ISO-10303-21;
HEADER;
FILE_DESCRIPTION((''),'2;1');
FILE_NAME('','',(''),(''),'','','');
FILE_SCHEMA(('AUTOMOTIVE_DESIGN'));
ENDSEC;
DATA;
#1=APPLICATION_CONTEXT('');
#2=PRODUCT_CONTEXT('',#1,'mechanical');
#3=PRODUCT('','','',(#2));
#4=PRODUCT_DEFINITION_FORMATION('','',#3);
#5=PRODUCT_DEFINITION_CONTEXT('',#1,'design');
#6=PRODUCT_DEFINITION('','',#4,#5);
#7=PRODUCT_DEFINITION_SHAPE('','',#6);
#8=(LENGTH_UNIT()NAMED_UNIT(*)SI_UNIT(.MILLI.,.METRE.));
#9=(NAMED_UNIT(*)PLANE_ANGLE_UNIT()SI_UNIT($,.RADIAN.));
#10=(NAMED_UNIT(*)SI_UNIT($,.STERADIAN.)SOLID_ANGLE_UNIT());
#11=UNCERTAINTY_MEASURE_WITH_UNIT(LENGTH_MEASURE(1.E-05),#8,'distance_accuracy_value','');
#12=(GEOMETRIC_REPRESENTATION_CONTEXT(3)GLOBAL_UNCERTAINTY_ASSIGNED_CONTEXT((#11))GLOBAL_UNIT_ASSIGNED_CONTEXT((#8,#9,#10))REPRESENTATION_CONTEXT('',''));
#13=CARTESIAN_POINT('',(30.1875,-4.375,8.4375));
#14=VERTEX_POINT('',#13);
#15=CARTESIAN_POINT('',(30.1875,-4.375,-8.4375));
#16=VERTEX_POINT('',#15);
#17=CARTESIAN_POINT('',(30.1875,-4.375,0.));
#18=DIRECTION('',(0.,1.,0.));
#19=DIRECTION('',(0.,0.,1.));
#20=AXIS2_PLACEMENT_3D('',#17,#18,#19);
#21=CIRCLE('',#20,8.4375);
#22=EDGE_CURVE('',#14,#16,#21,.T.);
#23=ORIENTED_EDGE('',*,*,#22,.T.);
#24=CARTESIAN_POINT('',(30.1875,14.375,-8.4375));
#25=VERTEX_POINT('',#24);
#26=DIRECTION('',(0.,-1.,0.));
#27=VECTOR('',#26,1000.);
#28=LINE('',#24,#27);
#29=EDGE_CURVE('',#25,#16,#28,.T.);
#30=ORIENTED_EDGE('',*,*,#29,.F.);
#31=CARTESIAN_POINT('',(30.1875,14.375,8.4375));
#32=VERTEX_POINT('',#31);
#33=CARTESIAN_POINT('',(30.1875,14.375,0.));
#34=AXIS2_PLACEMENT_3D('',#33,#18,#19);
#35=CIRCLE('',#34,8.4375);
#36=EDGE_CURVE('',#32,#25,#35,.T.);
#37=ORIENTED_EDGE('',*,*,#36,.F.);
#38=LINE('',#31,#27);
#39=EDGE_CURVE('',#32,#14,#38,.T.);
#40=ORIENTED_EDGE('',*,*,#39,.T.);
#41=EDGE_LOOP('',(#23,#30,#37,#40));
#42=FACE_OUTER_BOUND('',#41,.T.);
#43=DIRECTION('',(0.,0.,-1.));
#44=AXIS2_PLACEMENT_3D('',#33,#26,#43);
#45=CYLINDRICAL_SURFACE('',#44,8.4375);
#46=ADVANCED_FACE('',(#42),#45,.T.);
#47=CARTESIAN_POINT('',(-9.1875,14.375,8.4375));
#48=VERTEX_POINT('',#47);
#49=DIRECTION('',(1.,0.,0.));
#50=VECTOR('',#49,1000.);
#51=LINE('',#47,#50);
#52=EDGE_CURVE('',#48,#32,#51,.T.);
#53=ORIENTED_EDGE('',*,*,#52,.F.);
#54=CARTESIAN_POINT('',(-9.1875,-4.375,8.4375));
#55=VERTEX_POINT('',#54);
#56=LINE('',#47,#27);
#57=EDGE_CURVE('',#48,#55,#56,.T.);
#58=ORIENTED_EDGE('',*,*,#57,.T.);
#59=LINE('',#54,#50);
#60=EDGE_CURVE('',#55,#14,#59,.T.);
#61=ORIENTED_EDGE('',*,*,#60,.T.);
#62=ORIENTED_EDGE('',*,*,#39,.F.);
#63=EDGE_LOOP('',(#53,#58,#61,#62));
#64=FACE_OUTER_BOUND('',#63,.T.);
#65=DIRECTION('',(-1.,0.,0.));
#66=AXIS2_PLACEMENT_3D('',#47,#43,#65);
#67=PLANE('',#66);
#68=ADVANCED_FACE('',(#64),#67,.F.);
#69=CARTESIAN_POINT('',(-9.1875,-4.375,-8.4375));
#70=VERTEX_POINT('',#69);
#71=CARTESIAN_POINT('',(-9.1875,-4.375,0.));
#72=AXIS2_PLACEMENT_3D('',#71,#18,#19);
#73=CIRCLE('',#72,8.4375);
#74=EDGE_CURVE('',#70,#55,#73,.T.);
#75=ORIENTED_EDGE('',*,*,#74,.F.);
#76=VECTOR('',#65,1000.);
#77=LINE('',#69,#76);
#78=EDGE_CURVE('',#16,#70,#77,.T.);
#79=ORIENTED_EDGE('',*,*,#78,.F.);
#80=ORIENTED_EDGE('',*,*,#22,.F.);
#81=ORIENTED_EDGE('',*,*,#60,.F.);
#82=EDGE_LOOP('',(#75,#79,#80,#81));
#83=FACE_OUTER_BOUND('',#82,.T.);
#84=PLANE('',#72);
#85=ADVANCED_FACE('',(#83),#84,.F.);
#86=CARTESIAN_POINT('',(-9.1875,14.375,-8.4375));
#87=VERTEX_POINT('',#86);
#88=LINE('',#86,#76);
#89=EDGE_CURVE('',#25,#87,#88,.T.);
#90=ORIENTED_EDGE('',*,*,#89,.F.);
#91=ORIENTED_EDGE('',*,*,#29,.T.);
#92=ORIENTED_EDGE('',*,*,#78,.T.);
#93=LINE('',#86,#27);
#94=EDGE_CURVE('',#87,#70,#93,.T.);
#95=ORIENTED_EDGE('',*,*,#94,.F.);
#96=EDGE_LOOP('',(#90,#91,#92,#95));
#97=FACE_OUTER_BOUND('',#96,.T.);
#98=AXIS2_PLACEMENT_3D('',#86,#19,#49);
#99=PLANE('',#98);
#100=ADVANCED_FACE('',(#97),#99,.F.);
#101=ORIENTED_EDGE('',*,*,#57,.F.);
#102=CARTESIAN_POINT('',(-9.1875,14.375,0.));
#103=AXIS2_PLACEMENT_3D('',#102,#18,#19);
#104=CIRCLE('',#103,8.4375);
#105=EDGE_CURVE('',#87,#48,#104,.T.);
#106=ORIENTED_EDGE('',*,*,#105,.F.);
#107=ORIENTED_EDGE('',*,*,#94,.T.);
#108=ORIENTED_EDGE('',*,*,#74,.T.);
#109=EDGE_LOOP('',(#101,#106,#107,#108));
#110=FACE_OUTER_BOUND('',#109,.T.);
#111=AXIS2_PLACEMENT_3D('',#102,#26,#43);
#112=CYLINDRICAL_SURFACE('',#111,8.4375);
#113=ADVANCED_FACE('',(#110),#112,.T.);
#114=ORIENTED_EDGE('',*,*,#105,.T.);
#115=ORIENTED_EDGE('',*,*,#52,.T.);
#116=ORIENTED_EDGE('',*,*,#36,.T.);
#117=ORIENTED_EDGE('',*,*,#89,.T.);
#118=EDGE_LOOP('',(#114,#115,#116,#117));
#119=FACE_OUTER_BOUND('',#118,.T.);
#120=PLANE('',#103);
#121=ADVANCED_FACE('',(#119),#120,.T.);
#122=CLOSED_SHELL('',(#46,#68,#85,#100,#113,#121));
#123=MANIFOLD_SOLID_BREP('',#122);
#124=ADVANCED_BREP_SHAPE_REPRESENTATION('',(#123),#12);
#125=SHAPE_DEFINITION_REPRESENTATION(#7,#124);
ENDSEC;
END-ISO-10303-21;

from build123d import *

# Parameters (mm, degrees)
BOSS_EXTRUDE1_DEPTH = 10
SCALE_1_SCALE       = 1.875


with BuildPart() as part:
    # Sketch1 → Boss-Extrude1 (new body)
    with BuildSketch(Plane(origin=(0, 0, 0), x_dir=(1, 0, 0), z_dir=(0, 1, 0))):
        with BuildLine():
            Line((0, 4.5), (21, 4.5))
            ThreePointArc((21, 4.5), (25.5, 0), (21, -4.5))
            Line((21, -4.5), (0, -4.5))
            ThreePointArc((0, -4.5), (-4.5, 0), (0, 4.5))
        make_face()
    extrude(amount=BOSS_EXTRUDE1_DEPTH)


with BuildPart() as part_1:
    # Scale 1: scaled about (10.5, 5, 0)
    add(part.part.scale(SCALE_1_SCALE).moved(Location((-9.1875, -4.375, 0))))


solid = part_1.part
